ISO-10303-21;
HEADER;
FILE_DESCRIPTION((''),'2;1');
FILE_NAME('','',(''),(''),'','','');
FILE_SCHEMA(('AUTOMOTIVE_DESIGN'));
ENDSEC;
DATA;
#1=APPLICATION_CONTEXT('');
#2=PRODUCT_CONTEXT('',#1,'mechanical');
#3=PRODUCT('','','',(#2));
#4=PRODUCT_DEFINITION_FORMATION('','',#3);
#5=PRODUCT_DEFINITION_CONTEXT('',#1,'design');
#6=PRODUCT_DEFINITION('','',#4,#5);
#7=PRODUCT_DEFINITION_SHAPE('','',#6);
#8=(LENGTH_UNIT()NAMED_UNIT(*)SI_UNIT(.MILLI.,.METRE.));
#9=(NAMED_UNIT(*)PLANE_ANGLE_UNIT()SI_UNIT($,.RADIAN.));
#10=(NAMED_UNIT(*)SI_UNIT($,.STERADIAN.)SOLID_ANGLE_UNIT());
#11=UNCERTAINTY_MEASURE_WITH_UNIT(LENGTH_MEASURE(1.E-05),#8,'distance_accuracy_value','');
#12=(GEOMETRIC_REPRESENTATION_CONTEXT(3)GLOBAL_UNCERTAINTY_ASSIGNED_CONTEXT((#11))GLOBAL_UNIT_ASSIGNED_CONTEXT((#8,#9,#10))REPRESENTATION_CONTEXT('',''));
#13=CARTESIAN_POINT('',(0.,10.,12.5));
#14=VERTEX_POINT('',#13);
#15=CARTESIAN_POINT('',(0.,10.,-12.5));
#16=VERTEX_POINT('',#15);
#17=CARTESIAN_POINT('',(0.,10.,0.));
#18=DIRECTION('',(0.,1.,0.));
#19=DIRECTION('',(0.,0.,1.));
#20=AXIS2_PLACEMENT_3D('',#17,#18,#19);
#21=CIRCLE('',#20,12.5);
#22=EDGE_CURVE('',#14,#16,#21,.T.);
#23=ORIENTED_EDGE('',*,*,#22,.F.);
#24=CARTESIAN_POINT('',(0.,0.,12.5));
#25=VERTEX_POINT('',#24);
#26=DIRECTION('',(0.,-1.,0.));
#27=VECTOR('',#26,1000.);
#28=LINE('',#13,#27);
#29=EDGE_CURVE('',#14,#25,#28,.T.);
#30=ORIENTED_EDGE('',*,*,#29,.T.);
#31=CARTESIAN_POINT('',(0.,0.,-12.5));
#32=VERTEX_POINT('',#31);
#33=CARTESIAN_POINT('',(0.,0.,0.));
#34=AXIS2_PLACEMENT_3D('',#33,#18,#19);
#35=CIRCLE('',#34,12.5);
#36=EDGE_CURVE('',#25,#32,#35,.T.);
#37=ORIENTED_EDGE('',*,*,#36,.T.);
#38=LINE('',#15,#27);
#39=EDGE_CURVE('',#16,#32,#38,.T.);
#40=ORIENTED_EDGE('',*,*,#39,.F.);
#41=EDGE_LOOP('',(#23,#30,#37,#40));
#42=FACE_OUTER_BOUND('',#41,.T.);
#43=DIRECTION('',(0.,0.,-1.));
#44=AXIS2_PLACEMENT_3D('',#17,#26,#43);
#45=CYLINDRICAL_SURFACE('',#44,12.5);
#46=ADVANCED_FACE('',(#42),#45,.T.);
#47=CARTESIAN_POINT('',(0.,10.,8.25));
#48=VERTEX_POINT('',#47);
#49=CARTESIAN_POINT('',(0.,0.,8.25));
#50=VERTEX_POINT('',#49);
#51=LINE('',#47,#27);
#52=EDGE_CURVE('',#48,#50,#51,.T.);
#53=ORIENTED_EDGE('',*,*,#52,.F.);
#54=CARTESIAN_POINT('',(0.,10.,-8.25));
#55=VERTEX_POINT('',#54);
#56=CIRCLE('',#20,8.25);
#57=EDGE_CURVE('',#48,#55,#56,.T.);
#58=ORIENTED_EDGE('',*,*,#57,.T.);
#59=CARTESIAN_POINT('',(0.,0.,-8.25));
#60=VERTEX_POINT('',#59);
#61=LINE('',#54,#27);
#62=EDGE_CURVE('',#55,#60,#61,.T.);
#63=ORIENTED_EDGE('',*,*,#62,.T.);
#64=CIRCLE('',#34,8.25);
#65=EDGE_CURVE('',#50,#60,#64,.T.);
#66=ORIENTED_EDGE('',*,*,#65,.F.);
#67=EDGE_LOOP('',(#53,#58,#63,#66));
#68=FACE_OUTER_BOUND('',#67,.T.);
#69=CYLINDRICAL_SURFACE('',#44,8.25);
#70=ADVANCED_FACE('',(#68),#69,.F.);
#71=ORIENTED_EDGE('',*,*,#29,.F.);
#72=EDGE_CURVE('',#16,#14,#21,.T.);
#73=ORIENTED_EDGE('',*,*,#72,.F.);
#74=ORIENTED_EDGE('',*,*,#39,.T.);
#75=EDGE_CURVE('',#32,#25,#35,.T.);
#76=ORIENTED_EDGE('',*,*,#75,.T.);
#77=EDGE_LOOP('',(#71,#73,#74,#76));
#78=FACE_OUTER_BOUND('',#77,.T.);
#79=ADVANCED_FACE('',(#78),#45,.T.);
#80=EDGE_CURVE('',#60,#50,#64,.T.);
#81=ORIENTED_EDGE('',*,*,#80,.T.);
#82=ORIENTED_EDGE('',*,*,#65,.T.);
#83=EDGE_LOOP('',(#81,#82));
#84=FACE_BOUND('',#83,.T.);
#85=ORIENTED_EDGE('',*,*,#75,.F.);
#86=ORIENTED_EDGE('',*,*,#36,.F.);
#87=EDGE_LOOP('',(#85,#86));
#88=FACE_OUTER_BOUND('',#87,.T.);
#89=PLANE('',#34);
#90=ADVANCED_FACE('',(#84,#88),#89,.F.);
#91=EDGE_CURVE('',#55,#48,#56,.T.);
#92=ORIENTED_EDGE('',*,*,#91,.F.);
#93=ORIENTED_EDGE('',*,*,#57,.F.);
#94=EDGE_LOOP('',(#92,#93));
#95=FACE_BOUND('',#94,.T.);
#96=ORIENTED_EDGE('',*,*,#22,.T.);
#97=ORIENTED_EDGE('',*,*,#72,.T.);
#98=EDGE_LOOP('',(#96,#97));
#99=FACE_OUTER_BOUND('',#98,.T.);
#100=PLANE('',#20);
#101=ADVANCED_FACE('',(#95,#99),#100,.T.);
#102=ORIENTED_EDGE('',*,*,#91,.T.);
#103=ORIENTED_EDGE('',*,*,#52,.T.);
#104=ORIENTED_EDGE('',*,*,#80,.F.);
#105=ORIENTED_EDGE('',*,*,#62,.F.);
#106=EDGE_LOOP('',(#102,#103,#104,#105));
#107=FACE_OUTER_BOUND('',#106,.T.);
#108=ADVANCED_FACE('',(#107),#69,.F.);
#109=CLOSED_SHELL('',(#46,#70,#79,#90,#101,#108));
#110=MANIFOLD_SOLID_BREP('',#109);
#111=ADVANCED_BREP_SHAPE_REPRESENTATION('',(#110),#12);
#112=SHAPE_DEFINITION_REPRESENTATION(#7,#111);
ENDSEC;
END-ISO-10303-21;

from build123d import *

# Parameters (mm, degrees)
SKETCH1_R           = 12.5
SKETCH1_R_2         = 8.25
BOSS_EXTRUDE1_DEPTH = 10


with BuildPart() as part:
    # Sketch1 → Boss-Extrude1 (new body)
    with BuildSketch(Plane(origin=(0, 0, 0), x_dir=(1, 0, 0), z_dir=(0, 1, 0))):
        with Locations(Location((0, 0, 0), (0, 0, 270))):
            Circle(SKETCH1_R)
        with Locations(Location((0, 0, 0), (0, 0, 270))):
            Circle(SKETCH1_R_2, mode=Mode.SUBTRACT)
    extrude(amount=BOSS_EXTRUDE1_DEPTH)


solid = part.part
